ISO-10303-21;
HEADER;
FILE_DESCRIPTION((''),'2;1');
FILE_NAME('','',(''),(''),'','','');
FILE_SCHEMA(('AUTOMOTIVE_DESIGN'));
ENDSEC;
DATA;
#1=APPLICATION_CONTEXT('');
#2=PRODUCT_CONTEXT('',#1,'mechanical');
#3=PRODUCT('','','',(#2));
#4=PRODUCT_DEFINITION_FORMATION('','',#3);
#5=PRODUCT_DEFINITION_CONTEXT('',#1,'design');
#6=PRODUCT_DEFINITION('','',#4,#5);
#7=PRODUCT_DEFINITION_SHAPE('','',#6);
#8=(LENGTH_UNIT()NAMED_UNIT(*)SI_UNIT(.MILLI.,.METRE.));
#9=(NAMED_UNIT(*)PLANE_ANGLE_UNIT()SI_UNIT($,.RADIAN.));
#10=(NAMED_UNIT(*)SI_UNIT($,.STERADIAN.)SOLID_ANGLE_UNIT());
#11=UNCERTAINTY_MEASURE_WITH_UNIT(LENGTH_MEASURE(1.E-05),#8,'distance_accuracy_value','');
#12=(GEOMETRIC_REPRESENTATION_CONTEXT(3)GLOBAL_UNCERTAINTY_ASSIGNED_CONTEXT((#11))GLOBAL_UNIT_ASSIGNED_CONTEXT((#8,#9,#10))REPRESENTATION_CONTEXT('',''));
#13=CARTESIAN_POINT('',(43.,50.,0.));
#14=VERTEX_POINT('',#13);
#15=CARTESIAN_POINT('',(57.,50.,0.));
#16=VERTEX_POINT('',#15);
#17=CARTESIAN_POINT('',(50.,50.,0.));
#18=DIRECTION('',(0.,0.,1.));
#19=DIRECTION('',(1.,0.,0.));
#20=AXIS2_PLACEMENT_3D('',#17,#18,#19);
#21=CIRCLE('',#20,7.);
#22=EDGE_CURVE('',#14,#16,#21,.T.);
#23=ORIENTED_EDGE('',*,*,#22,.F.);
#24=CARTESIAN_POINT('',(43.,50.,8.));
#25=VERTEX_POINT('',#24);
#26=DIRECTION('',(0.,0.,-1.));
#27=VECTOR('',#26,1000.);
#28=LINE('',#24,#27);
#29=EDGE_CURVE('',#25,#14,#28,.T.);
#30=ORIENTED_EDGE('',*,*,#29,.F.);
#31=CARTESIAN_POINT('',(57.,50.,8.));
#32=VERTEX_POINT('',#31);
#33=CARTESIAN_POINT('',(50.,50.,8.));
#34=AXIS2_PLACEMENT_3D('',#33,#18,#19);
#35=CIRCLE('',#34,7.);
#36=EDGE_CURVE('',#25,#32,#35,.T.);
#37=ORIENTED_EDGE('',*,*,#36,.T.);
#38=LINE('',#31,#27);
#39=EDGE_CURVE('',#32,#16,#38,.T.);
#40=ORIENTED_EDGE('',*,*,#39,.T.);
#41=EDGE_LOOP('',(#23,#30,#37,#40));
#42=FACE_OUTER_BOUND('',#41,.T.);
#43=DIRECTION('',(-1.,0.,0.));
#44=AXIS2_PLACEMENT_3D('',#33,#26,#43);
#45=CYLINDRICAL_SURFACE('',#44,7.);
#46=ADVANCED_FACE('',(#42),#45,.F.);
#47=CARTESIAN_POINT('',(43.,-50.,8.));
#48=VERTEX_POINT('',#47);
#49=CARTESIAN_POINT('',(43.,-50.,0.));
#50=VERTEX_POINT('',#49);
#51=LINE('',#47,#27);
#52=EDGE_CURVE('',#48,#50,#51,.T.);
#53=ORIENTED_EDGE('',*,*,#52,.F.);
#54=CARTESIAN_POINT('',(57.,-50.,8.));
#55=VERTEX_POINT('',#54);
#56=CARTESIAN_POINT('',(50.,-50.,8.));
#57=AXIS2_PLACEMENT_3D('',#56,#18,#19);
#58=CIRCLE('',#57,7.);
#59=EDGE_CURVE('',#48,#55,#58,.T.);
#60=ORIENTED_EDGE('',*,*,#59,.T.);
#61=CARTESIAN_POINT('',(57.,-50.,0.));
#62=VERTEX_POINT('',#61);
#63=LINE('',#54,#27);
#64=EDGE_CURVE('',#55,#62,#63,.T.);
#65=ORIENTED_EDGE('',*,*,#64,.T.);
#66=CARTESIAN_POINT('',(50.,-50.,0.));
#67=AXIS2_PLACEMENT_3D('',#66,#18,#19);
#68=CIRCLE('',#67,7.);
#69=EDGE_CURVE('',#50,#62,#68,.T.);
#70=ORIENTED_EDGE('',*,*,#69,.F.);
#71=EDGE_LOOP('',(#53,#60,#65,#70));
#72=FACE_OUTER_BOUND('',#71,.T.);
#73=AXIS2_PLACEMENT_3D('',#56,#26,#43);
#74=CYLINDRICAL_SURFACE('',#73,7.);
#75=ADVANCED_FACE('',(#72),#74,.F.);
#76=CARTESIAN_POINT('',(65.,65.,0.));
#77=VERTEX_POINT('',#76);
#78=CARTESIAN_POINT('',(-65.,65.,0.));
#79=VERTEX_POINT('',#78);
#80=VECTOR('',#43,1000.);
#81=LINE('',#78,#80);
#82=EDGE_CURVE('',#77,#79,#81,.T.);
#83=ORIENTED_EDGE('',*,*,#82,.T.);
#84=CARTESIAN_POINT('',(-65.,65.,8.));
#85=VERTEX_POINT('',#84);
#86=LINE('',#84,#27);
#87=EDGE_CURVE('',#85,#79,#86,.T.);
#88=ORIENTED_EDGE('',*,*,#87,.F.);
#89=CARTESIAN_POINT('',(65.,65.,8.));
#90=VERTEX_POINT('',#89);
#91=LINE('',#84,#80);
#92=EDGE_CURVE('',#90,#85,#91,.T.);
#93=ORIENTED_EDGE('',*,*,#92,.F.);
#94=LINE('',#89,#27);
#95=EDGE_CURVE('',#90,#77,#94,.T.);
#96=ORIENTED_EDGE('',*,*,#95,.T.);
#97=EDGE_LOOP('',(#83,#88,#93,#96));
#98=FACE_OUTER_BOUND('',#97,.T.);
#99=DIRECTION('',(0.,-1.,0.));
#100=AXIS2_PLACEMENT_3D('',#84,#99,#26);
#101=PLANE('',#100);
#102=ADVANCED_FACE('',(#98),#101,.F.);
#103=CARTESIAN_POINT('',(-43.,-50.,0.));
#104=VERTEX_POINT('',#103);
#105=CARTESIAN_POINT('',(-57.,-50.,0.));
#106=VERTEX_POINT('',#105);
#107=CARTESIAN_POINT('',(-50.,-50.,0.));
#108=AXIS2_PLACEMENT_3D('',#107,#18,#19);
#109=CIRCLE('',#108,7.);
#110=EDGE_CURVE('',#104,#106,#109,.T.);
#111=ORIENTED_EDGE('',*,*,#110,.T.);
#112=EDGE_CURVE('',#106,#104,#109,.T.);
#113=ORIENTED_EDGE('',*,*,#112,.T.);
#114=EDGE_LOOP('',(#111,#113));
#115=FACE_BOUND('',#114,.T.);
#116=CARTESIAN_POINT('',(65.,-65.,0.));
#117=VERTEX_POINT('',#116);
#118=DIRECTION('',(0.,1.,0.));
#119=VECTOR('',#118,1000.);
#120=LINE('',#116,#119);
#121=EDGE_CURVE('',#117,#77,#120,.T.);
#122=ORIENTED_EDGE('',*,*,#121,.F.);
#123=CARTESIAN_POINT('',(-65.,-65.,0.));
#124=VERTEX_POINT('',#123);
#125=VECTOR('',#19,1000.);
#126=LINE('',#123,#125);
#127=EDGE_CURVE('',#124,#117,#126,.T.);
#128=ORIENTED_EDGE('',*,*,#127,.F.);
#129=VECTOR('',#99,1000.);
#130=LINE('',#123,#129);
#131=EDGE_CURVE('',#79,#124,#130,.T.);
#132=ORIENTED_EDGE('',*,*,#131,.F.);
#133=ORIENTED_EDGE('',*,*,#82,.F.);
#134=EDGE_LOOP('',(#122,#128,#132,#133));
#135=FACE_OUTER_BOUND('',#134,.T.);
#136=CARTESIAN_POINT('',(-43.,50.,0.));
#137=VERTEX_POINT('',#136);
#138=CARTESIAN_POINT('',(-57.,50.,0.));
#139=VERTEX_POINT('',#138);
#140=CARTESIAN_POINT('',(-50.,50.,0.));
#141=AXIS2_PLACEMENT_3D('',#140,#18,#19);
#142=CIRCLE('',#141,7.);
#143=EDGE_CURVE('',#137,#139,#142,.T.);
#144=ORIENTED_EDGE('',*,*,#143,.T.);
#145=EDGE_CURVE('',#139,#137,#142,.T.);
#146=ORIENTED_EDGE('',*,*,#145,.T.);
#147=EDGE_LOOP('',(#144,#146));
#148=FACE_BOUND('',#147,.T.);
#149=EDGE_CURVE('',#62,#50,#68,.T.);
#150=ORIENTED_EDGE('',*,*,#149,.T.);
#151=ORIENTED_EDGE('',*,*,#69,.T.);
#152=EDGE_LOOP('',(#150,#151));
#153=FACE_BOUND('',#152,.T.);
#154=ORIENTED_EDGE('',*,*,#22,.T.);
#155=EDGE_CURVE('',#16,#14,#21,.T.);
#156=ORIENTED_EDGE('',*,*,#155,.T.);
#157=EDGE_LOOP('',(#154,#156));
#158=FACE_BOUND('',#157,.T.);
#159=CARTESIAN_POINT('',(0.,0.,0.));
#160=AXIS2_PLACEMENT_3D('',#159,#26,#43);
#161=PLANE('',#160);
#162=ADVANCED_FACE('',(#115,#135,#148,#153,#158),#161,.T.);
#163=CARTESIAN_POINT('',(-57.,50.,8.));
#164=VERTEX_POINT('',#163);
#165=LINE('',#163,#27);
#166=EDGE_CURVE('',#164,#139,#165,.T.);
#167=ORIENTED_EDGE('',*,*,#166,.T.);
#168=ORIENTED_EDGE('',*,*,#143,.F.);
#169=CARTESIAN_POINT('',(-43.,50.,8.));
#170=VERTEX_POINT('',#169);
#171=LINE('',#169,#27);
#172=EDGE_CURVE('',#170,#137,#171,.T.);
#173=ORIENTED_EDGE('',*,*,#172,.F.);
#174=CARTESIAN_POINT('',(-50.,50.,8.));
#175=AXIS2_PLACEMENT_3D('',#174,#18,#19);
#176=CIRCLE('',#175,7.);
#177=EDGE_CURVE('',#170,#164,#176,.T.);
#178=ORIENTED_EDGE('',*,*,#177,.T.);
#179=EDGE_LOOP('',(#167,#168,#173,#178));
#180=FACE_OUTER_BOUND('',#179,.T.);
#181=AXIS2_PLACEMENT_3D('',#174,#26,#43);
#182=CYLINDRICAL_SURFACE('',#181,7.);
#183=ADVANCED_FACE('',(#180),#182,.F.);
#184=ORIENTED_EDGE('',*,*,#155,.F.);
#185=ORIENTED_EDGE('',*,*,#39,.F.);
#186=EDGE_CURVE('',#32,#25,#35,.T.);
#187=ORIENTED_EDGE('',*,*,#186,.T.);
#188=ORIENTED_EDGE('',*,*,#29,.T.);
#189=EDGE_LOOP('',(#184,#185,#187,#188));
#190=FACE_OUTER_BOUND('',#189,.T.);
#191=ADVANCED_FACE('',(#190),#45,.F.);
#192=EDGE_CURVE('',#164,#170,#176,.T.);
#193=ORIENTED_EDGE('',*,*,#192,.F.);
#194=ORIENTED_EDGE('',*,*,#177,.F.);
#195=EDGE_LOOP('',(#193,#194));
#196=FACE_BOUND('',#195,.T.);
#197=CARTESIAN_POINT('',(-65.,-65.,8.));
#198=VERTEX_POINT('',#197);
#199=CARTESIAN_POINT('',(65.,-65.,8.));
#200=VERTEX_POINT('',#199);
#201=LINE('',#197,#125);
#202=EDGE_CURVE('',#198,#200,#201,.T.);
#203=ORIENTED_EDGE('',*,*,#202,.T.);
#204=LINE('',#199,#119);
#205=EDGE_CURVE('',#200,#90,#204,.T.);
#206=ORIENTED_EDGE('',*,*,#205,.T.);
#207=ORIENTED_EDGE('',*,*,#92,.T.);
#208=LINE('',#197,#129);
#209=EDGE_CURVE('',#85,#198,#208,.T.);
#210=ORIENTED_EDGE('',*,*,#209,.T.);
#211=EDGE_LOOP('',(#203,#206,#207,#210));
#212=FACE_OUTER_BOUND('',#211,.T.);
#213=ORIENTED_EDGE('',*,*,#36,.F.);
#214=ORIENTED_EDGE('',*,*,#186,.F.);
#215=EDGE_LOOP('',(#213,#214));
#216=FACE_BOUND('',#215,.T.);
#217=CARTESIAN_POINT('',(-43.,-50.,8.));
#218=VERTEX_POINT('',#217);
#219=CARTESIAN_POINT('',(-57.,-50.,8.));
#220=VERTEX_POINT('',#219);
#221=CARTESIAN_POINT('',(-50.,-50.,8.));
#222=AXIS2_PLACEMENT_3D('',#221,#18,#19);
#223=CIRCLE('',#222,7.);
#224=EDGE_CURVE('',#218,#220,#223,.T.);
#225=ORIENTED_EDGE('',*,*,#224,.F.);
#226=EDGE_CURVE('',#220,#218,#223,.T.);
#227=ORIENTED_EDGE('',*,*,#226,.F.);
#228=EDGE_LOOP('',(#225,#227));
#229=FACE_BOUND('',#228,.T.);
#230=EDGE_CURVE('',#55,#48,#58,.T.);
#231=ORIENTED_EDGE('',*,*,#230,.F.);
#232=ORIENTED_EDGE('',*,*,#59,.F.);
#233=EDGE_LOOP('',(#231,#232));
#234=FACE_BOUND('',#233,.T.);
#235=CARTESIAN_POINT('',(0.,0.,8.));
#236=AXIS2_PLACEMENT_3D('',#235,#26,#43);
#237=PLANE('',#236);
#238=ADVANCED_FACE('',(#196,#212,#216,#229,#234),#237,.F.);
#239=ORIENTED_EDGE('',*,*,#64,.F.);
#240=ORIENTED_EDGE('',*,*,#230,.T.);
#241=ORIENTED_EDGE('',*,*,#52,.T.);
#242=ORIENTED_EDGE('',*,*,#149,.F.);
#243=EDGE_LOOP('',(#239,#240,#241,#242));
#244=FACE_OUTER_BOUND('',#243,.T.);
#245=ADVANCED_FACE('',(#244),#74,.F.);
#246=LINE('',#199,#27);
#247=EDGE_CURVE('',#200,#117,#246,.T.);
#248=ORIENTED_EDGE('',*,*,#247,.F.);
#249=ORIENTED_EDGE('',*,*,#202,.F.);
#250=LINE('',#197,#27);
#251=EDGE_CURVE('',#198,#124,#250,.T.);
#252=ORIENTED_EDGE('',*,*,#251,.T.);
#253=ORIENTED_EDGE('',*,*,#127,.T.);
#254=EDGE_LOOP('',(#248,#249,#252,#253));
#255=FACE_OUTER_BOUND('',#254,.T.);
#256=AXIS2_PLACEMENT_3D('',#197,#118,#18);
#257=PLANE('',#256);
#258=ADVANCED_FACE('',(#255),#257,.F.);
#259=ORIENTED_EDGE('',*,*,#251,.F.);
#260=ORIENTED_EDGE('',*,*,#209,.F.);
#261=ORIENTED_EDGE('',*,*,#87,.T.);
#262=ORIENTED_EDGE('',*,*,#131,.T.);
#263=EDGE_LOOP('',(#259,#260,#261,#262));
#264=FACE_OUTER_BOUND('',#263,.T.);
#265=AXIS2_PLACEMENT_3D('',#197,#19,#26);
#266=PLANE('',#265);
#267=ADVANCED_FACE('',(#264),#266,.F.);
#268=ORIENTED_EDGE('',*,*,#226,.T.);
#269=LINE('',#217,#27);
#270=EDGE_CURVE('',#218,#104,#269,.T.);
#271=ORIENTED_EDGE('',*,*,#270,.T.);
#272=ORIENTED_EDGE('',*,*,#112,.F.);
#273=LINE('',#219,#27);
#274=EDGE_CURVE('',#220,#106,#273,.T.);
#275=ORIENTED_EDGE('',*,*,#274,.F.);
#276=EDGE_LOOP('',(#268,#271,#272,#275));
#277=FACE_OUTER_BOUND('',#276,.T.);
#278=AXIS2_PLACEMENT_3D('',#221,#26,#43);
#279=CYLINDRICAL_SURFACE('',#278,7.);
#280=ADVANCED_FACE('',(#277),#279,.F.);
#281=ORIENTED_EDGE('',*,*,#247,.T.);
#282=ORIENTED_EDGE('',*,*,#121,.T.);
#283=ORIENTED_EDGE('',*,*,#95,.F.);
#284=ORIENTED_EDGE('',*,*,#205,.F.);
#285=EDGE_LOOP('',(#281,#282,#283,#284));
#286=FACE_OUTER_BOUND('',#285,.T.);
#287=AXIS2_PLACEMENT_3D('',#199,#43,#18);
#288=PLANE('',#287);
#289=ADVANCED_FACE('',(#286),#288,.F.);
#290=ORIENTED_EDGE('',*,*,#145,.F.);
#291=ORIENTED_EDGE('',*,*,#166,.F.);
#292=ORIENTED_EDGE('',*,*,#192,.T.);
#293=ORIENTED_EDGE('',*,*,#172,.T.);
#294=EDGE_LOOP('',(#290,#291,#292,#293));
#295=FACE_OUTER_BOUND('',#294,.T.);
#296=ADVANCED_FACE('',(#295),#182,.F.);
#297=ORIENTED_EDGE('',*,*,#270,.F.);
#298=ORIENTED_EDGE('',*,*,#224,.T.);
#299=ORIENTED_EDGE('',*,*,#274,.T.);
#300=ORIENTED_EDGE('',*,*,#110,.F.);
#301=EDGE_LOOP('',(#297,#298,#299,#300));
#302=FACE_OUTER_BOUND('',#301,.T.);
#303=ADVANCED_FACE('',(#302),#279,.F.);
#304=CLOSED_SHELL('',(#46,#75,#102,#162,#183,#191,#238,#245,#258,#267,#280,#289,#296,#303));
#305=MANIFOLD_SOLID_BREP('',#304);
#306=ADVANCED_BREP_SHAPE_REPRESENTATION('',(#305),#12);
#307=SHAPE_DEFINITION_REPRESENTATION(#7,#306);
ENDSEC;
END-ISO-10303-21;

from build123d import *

# Parameters (mm, degrees)
SKETCH1_W           = 130
SKETCH1_H           = 130
SKETCH1_R           = 7
BOSS_EXTRUDE1_DEPTH = 8


with BuildPart() as part:
    # Sketch1 → Boss-Extrude1 (new body)
    with BuildSketch(Plane.XY):
        Rectangle(SKETCH1_W, SKETCH1_H)
        with Locations((-50, 50)):
            Circle(SKETCH1_R, mode=Mode.SUBTRACT)
        with Locations((50, 50)):
            Circle(SKETCH1_R, mode=Mode.SUBTRACT)
        with Locations((50, -50)):
            Circle(SKETCH1_R, mode=Mode.SUBTRACT)
        with Locations((-50, -50)):
            Circle(SKETCH1_R, mode=Mode.SUBTRACT)
    extrude(amount=BOSS_EXTRUDE1_DEPTH)


solid = part.part
